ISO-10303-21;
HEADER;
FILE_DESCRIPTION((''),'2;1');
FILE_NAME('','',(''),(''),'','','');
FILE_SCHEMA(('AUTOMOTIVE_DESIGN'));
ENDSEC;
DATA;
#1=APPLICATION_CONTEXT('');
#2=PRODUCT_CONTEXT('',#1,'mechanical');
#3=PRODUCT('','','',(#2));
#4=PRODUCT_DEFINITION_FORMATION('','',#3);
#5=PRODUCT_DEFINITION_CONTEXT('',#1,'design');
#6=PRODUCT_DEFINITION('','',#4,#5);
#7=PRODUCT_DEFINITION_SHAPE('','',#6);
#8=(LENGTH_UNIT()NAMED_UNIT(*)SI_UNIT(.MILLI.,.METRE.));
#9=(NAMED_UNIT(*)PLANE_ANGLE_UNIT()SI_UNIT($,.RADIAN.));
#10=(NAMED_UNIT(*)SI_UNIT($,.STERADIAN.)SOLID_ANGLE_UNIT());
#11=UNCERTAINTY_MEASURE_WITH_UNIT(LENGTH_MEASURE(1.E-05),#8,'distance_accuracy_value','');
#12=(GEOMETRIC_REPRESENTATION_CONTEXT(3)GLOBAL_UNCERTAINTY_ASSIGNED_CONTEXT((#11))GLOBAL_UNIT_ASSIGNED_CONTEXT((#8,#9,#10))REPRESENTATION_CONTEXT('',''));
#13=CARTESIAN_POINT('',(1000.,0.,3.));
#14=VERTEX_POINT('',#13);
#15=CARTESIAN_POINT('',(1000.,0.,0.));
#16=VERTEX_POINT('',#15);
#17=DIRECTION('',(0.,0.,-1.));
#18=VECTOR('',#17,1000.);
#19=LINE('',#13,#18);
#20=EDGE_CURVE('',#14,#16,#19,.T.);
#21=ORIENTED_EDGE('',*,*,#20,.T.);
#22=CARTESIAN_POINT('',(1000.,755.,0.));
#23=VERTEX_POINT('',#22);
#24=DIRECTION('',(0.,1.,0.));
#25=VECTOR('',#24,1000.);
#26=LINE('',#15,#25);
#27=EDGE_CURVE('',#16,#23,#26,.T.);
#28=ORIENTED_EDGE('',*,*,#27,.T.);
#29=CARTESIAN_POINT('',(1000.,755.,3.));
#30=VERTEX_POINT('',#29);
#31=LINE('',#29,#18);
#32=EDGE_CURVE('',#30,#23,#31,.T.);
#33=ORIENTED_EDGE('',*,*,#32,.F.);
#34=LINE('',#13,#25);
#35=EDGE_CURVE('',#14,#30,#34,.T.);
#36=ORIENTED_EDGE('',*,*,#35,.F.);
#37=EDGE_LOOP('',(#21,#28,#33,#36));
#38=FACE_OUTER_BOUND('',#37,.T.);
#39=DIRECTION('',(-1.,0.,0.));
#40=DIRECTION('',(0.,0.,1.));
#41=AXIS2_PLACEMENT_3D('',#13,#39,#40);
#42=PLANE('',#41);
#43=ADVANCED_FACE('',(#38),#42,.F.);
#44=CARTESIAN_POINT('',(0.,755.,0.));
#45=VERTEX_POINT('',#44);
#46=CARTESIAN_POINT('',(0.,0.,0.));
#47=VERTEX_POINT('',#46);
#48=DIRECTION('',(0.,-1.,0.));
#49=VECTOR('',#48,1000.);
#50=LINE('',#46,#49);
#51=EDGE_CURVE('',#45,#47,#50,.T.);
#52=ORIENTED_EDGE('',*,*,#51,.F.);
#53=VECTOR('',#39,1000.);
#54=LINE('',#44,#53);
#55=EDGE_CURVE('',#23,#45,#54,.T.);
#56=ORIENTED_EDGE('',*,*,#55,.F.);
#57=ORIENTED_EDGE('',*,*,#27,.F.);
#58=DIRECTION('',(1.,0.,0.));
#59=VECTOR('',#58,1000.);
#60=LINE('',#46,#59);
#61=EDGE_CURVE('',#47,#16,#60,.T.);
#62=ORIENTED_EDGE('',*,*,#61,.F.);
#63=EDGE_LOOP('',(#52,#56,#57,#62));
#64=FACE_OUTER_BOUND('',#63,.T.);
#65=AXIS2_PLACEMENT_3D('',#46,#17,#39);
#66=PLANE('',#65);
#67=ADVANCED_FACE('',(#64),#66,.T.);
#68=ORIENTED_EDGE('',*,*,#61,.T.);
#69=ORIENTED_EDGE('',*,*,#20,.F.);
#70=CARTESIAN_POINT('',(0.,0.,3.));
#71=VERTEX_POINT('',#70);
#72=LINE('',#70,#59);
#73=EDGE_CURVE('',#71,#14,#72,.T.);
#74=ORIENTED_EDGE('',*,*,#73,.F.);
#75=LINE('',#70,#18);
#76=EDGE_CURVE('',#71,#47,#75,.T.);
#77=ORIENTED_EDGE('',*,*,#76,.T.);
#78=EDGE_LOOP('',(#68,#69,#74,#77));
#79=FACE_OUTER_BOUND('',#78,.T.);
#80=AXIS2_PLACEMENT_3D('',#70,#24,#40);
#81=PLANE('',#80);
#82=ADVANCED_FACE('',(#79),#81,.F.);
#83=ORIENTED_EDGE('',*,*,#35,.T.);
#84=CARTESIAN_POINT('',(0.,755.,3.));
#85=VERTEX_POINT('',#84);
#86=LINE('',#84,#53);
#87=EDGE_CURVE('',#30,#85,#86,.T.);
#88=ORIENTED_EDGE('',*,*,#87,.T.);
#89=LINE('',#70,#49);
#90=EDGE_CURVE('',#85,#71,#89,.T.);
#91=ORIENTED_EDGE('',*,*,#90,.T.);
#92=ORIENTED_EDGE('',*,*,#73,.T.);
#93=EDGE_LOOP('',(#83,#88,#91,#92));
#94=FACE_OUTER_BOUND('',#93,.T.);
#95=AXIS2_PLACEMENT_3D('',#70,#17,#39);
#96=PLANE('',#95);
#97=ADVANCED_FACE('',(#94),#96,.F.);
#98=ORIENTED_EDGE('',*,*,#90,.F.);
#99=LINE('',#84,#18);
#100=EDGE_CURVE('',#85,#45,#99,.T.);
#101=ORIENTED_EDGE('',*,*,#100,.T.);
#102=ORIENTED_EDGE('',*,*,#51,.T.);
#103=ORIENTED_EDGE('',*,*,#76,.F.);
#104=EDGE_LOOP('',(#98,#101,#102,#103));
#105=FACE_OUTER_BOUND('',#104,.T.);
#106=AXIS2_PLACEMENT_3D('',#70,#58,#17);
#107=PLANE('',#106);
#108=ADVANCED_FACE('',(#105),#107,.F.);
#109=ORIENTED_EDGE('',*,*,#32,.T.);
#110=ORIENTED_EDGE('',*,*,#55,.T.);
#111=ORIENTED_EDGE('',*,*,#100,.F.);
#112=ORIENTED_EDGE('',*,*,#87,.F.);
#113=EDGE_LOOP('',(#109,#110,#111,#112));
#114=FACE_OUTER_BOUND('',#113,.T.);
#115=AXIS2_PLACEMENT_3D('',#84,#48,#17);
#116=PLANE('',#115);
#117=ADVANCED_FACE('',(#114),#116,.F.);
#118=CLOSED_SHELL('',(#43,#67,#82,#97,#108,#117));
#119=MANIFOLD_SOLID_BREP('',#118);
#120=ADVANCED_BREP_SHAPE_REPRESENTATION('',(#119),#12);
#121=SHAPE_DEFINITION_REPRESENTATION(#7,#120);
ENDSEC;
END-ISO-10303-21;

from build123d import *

# Parameters (mm, degrees)
SKETCH1_W           = 1000
SKETCH1_H           = 755
BOSS_EXTRUDE1_DEPTH = 3


with BuildPart() as part:
    # Sketch1 → Boss-Extrude1 (new body)
    with BuildSketch(Plane.XY):
        with Locations((500, 377.5)):
            Rectangle(SKETCH1_W, SKETCH1_H)
    extrude(amount=BOSS_EXTRUDE1_DEPTH)


solid = part.part
